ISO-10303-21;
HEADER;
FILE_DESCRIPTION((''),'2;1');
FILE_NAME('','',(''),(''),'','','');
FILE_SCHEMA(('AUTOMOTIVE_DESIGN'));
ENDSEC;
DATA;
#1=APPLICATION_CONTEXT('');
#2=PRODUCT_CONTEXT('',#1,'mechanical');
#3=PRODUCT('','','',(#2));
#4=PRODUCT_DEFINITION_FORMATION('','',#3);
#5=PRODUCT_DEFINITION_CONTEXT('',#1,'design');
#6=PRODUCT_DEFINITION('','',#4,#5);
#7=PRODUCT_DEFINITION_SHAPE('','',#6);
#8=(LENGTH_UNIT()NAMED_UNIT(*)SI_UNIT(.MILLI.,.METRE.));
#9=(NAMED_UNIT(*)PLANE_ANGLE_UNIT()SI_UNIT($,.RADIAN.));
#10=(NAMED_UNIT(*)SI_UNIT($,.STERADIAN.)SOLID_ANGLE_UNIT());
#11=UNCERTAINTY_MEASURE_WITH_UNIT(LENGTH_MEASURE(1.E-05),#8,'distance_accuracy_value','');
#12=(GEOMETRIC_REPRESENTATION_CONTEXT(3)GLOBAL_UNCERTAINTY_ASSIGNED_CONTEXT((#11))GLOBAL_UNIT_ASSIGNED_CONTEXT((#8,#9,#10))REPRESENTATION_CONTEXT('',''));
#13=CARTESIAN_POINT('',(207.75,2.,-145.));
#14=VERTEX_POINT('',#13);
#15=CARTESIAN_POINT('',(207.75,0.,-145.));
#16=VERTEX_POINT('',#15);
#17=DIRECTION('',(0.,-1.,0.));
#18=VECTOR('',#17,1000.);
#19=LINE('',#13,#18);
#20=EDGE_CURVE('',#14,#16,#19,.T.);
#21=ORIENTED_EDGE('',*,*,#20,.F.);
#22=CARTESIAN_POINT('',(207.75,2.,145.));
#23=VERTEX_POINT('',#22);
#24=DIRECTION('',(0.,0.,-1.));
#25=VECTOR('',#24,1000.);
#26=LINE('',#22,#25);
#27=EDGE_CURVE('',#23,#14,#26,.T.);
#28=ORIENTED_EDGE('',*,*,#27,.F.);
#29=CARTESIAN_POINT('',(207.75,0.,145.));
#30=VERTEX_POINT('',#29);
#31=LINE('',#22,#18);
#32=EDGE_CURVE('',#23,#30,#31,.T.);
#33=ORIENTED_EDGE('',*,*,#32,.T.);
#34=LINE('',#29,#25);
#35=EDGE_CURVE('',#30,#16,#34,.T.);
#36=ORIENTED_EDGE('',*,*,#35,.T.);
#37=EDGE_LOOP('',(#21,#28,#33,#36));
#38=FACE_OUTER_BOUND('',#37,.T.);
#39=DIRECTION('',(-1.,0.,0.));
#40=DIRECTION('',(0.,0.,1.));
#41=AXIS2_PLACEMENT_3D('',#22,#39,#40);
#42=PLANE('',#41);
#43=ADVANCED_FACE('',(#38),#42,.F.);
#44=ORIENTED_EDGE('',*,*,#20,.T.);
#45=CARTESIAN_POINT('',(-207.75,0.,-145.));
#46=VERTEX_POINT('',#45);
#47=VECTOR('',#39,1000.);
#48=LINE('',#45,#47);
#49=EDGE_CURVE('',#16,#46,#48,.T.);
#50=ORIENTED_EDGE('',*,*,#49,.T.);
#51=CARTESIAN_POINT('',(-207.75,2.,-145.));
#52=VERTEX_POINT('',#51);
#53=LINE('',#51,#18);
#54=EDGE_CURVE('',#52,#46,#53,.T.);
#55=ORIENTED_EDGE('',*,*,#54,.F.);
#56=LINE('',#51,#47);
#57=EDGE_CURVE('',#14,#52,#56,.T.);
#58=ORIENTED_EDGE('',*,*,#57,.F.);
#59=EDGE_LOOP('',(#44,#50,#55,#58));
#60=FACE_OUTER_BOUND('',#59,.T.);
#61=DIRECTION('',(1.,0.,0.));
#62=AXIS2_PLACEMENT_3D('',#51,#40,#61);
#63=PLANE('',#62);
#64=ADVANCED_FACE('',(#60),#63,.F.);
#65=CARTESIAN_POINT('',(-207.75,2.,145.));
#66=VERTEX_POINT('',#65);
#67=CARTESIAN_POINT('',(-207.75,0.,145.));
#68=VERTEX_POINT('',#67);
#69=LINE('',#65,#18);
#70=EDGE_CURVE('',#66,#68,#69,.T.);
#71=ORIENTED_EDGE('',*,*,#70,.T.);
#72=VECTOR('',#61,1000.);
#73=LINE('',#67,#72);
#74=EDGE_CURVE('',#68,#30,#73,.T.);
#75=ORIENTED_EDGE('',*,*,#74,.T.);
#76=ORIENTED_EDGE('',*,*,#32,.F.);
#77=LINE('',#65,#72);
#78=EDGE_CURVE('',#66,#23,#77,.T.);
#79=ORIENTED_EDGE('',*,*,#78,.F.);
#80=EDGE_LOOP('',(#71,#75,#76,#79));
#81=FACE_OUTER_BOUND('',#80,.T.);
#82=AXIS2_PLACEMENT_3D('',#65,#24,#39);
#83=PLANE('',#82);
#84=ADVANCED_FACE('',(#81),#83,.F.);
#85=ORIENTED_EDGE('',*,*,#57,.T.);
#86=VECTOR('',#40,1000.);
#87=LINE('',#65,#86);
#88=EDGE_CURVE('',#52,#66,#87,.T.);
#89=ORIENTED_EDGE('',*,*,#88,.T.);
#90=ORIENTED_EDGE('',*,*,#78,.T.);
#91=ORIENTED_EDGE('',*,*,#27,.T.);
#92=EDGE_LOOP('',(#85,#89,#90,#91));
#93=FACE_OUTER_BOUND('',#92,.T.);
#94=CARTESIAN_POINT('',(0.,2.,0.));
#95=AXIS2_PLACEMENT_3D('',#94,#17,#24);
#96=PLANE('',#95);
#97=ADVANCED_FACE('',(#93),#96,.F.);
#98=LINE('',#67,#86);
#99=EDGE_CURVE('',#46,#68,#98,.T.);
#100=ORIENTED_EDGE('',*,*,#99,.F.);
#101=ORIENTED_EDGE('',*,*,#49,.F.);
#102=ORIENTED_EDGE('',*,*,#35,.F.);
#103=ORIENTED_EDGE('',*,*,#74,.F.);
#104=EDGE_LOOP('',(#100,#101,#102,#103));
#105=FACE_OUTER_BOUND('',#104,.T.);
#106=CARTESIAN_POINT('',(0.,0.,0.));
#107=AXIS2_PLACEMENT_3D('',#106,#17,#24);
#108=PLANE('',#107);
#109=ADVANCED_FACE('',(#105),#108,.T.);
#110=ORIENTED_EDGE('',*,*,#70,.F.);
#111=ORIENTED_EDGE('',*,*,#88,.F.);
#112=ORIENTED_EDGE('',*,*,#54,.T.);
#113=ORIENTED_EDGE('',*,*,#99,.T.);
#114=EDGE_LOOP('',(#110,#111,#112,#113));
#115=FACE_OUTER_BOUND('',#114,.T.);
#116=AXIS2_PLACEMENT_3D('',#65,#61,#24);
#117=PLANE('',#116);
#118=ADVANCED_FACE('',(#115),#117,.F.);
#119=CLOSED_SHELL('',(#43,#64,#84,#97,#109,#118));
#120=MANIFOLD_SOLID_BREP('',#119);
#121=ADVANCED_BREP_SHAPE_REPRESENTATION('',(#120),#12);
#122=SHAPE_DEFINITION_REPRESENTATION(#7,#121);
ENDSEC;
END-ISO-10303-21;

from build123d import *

# Parameters (mm, degrees)
SKETCH_1_W      = 415.5
SKETCH_1_H      = 290
EXTRUDE_1_DEPTH = 2


with BuildPart() as part:
    # 草图1 → 凸台-拉伸1 (new body)
    with BuildSketch(Plane(origin=(0, 0, 0), x_dir=(1, 0, 0), z_dir=(0, 1, 0))):
        Rectangle(SKETCH_1_W, SKETCH_1_H)
    extrude(amount=EXTRUDE_1_DEPTH)


solid = part.part
